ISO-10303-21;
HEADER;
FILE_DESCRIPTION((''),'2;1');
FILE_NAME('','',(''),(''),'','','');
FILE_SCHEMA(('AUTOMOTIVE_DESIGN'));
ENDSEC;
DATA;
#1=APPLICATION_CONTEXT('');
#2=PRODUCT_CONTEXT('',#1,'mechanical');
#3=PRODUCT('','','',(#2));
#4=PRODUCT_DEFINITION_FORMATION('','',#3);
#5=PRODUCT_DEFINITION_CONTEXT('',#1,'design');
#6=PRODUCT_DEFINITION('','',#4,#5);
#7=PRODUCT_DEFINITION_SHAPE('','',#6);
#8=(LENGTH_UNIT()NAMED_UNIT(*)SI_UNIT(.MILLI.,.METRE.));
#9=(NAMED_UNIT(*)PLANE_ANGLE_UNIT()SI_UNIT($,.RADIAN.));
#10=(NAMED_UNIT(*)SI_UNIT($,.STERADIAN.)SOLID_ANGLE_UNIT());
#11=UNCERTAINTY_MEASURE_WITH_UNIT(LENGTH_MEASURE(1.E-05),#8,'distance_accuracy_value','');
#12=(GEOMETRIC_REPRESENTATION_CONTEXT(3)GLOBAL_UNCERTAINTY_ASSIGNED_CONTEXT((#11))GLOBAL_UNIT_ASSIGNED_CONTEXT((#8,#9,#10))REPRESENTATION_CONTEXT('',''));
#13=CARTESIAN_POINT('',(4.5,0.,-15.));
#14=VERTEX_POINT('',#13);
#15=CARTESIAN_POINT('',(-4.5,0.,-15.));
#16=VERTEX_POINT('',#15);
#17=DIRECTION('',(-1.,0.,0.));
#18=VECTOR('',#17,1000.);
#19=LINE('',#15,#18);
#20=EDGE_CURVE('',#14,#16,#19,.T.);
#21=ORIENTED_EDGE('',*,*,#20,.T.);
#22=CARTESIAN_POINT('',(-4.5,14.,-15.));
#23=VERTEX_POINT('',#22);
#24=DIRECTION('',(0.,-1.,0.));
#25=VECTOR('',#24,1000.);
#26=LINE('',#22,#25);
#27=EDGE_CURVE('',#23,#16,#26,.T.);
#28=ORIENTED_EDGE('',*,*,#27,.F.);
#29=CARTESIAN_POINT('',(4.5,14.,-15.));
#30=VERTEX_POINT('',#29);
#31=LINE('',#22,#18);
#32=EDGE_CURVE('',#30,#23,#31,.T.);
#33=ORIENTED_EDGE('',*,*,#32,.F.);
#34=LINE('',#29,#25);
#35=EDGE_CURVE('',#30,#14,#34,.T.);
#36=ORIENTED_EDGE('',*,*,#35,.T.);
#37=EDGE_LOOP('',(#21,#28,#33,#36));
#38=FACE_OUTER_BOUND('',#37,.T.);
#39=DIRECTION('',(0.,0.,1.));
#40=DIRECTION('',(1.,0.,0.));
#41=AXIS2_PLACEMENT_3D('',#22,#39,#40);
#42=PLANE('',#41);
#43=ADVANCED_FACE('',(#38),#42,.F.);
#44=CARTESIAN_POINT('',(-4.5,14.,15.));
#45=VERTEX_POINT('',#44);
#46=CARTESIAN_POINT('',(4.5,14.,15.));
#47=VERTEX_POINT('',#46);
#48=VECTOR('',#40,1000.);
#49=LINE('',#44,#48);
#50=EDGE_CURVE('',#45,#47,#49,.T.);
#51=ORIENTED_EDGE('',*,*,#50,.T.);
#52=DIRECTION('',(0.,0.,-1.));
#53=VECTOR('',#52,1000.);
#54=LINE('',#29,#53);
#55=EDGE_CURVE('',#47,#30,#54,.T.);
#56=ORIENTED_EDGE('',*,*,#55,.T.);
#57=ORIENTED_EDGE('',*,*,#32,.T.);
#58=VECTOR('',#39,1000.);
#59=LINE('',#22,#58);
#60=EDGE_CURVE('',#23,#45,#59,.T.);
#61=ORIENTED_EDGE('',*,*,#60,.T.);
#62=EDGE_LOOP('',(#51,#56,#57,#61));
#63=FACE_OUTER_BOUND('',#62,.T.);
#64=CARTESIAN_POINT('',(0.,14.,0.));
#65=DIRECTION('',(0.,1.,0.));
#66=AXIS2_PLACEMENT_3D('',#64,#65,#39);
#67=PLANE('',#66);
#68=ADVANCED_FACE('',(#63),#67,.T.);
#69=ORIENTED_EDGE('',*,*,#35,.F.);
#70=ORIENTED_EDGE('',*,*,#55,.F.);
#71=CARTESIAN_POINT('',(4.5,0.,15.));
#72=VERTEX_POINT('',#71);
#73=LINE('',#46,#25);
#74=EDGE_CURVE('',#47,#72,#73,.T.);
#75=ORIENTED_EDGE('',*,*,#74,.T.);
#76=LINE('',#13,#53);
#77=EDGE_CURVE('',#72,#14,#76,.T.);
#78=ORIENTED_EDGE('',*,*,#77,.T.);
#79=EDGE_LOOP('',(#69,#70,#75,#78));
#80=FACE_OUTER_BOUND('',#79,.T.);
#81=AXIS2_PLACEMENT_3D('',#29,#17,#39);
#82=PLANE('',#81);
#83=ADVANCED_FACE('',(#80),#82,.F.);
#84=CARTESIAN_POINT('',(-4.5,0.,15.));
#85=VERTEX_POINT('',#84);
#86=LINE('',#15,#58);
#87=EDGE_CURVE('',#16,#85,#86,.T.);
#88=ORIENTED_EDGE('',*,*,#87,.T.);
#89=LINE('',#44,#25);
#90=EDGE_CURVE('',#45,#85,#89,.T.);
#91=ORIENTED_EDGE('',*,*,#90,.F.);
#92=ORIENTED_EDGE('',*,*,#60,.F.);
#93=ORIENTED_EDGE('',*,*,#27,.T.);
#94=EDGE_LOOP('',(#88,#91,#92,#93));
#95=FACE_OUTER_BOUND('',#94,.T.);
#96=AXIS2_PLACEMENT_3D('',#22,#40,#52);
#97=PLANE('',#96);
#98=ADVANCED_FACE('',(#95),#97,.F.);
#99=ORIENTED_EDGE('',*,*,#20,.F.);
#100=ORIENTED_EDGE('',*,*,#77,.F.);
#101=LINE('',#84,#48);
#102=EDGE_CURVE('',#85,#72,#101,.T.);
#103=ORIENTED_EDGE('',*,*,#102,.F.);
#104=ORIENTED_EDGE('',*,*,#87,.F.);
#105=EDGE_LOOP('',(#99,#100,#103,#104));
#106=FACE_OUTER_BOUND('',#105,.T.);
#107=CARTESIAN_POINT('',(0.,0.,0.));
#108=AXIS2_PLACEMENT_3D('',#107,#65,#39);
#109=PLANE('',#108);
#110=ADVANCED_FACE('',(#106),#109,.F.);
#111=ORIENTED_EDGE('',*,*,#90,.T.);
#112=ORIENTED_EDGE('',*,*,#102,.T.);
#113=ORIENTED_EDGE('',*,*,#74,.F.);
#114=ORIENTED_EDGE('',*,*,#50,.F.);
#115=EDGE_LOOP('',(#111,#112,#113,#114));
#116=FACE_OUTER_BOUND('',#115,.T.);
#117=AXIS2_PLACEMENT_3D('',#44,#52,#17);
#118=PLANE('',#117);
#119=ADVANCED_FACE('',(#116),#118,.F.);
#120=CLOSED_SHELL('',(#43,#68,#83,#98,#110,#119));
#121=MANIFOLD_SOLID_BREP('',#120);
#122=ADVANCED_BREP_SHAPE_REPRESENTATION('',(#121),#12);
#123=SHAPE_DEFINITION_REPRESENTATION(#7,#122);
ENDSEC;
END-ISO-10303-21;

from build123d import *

# Parameters (mm, degrees)
SKETCH1_W           = 9
SKETCH1_H           = 30
BOSS_EXTRUDE1_DEPTH = 14


with BuildPart() as part:
    # Sketch1 → Boss-Extrude1 (new body)
    with BuildSketch(Plane(origin=(0, 0, 0), x_dir=(1, 0, 0), z_dir=(0, 1, 0))):
        Rectangle(SKETCH1_W, SKETCH1_H)
    extrude(amount=BOSS_EXTRUDE1_DEPTH)


solid = part.part
